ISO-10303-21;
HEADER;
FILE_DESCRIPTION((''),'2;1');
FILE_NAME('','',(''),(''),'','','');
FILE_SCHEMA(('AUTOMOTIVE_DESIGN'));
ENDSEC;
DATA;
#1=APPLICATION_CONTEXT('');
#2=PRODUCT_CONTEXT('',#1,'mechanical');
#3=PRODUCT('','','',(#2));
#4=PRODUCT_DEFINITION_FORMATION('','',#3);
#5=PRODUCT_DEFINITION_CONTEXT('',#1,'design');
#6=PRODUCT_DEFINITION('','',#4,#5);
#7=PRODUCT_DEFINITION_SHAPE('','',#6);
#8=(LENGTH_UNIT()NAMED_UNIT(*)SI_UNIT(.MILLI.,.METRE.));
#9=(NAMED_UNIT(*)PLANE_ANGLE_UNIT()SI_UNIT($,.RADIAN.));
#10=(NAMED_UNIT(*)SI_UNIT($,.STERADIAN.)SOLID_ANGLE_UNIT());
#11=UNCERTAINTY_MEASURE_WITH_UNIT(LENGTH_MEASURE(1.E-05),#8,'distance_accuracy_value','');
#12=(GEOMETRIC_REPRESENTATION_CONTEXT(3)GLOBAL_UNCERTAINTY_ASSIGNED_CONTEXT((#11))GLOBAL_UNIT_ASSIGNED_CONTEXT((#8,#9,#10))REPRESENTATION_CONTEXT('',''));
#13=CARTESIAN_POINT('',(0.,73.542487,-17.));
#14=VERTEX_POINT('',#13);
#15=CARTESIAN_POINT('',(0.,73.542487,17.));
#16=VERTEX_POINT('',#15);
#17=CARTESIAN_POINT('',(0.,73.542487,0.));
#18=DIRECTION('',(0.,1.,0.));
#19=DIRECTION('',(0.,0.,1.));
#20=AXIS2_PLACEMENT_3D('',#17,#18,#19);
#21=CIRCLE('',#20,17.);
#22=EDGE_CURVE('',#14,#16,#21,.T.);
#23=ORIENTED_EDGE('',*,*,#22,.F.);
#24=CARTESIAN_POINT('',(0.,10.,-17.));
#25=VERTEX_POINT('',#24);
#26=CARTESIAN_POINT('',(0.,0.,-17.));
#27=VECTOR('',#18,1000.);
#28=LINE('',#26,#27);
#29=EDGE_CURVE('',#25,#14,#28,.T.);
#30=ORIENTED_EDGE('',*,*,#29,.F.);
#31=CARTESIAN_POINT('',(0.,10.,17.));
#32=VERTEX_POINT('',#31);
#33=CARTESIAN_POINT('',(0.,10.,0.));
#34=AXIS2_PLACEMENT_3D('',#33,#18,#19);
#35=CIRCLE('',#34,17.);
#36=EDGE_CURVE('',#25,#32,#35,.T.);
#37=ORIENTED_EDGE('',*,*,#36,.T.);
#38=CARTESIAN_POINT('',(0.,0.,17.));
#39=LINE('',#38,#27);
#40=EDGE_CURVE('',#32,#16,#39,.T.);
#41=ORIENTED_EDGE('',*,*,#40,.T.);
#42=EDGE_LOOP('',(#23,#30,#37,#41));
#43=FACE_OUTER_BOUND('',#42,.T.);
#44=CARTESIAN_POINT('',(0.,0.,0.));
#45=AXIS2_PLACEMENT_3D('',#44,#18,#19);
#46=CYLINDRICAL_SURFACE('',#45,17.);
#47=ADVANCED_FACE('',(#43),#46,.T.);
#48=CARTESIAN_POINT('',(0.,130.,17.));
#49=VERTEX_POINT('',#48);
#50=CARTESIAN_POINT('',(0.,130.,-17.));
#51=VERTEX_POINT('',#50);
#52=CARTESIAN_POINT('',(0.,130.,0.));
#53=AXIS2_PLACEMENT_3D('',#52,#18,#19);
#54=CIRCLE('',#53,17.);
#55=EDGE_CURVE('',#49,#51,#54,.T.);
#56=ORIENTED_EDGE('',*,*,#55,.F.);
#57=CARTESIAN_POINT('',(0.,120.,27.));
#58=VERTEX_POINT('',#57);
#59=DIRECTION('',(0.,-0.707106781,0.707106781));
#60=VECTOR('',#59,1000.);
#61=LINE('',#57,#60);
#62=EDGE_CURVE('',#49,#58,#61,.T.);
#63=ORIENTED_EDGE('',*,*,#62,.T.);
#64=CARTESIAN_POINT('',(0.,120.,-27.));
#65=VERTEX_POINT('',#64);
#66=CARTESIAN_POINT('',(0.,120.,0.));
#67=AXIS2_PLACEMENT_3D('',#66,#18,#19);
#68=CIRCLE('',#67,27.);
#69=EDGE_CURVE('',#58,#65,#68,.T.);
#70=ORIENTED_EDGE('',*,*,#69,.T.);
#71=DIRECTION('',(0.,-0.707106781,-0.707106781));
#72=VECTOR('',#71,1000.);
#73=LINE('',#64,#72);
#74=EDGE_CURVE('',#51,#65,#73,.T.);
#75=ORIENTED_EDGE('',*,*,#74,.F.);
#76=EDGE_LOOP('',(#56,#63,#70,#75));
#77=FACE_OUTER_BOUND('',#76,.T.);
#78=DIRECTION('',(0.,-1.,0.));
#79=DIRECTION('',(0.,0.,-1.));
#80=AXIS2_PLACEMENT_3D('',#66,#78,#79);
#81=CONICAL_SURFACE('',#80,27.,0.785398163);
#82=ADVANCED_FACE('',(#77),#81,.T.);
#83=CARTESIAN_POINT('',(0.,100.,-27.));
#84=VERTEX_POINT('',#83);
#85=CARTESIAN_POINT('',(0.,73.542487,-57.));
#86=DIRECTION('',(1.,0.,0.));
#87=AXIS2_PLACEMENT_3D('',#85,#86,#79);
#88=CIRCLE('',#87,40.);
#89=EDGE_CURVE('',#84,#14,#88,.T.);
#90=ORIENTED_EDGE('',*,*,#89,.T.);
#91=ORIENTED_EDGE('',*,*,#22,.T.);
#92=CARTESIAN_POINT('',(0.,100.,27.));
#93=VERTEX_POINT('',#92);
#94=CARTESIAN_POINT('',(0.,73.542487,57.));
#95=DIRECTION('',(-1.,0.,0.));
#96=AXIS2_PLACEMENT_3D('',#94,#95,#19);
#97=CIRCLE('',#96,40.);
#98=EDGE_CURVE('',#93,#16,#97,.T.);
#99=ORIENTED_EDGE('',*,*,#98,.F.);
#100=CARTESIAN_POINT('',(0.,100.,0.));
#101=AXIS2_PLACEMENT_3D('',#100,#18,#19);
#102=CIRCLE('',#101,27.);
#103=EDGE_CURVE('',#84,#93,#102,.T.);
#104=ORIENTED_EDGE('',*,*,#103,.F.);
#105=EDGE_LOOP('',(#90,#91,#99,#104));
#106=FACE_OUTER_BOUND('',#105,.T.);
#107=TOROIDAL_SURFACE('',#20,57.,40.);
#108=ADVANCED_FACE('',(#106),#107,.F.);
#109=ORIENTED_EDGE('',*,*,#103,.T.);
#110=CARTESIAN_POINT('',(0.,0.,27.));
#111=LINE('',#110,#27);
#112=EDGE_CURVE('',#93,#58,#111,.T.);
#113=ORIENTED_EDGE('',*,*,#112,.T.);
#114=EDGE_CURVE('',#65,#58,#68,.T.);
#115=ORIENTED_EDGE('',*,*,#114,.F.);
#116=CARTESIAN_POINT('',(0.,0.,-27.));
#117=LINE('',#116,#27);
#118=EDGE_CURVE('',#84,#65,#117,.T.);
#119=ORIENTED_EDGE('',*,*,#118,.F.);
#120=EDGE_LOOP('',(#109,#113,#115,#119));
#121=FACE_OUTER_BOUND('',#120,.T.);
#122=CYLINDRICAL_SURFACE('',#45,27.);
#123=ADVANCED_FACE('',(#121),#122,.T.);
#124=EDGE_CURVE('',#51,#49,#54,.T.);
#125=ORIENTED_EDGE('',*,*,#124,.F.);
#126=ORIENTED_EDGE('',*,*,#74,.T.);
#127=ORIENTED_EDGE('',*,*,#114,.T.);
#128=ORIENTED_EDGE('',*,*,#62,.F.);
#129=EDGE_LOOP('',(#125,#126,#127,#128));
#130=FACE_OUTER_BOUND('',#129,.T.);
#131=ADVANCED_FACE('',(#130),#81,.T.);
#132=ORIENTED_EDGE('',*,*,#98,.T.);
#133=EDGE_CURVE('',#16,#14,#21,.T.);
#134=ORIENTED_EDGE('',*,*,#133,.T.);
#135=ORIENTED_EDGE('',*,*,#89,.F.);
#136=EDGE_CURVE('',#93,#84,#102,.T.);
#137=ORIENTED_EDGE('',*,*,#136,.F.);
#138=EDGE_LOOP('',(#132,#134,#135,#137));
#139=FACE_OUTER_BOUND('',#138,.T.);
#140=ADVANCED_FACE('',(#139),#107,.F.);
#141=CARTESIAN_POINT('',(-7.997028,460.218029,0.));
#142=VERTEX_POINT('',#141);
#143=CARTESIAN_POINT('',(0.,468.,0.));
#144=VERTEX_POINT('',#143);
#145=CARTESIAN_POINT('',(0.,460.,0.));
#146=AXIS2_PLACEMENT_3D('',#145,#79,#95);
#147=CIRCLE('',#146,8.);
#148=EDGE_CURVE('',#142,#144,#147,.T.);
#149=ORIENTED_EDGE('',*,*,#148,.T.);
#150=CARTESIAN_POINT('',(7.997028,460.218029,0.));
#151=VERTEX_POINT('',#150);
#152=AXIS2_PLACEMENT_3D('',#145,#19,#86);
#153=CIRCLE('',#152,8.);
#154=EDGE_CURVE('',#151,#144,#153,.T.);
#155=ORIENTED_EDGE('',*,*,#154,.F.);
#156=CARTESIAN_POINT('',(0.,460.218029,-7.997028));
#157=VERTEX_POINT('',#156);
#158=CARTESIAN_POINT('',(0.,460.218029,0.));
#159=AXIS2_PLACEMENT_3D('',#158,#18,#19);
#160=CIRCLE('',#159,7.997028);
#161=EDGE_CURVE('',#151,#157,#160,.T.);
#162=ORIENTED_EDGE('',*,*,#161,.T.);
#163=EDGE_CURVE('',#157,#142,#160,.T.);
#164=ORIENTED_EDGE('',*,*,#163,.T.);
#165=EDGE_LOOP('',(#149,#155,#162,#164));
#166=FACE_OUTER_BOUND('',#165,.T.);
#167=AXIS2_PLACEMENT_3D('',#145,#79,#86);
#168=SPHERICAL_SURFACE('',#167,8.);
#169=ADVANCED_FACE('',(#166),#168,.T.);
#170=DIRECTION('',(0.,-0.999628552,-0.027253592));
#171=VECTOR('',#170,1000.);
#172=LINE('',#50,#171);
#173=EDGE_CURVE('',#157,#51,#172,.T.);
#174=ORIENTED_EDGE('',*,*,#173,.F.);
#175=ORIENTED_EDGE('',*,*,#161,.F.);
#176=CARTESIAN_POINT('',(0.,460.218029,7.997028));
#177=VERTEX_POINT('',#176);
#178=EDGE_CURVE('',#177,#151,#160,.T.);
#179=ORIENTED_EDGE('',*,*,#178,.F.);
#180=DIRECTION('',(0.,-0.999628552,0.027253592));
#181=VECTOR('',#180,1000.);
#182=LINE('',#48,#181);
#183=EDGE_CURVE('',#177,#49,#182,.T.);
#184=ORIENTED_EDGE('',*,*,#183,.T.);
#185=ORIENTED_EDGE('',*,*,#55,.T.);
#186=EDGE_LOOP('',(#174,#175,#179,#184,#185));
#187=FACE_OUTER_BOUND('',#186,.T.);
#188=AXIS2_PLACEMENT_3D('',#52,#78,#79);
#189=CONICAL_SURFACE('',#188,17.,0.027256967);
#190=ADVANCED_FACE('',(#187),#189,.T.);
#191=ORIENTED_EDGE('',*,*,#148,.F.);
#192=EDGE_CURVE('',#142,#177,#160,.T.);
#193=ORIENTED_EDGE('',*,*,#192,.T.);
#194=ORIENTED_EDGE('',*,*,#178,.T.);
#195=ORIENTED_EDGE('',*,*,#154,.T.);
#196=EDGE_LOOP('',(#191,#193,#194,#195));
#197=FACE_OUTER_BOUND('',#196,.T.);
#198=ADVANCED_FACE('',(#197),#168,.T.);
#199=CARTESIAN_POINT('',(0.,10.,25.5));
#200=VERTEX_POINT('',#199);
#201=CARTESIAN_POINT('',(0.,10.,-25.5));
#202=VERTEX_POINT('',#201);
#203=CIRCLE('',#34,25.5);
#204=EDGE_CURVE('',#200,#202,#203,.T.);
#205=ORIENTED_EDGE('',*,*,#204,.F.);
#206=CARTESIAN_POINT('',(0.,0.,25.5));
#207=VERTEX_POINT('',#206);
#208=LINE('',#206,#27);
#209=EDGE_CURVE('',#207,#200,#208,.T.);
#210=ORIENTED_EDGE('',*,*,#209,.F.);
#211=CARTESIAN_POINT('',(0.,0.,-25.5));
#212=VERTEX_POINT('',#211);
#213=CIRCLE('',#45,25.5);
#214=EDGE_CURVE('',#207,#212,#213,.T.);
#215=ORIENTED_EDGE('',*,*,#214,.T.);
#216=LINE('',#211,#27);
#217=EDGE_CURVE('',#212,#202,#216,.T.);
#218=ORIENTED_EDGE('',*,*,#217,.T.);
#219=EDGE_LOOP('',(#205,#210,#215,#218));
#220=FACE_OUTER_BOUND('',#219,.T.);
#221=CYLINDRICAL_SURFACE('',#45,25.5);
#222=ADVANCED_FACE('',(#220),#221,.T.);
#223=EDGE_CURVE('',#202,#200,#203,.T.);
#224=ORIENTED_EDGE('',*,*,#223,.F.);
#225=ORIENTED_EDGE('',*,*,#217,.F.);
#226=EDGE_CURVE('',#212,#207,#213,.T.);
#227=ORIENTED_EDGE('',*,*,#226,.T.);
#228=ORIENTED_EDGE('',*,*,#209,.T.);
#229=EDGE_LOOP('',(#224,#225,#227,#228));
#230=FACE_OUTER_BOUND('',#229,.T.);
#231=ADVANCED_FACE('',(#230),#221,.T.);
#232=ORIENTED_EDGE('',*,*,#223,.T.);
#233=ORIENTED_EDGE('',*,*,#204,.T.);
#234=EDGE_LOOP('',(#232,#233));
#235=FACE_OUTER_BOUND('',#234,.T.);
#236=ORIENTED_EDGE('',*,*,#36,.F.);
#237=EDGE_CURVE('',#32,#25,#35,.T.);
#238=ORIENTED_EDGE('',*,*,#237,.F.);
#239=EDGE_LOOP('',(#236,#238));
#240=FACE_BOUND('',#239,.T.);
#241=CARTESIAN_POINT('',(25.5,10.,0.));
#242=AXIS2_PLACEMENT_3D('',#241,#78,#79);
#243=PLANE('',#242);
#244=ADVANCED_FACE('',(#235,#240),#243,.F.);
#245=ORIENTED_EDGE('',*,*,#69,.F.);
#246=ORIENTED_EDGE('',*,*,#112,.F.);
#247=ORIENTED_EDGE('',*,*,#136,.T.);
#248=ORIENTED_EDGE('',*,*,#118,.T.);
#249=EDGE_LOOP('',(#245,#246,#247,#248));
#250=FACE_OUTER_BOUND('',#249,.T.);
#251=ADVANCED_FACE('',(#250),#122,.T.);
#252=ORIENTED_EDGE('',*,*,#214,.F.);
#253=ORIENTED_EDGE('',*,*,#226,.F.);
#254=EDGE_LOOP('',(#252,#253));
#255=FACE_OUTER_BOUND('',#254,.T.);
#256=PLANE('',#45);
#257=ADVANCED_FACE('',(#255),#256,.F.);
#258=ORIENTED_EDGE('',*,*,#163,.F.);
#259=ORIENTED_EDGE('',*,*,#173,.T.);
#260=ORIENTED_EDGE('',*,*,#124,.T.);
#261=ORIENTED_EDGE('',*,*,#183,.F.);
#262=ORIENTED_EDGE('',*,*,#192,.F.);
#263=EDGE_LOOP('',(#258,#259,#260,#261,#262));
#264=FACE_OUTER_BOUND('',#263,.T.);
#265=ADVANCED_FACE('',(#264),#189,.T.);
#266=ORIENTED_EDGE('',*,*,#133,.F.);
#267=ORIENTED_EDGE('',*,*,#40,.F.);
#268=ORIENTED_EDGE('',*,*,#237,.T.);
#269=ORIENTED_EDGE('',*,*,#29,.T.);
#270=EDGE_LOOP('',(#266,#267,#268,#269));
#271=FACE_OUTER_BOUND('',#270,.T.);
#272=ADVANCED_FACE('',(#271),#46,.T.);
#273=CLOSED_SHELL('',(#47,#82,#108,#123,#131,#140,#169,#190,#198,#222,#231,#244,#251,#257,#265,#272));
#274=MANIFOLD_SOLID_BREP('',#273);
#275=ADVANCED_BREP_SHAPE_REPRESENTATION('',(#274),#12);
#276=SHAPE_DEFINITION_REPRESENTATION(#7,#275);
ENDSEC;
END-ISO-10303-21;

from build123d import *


with BuildPart() as part:
    # Sketch1 → Revolve1 (revolve)
    with BuildSketch(Plane.XY, mode=Mode.PRIVATE) as revolve1_sk:
        with BuildLine():
            Line((0, 0), (25.5, 0))
            Line((25.5, 0), (25.5, 10))
            Line((25.5, 10), (17, 10))
            Line((17, 10), (17, 73.542486889))
            ThreePointArc((17, 73.542486889), (19.583426132, 87.684622513), (27, 100))
            Line((27, 100), (27, 120))
            Line((27, 120), (17, 130))
            Line((17, 130), (7.997028415, 460.218028737))
            ThreePointArc((7.997028415, 460.218028737), (5.57923696, 465.733420876), (0, 468))
            Line((0, 468), (0, 0))
        make_face()
    revolve(revolve1_sk.sketch.rotate(Axis((0, 0, 0), (0, -1, 0)), 90), axis=Axis((0, 0, 0), (0, -1, 0)))


solid = part.part
